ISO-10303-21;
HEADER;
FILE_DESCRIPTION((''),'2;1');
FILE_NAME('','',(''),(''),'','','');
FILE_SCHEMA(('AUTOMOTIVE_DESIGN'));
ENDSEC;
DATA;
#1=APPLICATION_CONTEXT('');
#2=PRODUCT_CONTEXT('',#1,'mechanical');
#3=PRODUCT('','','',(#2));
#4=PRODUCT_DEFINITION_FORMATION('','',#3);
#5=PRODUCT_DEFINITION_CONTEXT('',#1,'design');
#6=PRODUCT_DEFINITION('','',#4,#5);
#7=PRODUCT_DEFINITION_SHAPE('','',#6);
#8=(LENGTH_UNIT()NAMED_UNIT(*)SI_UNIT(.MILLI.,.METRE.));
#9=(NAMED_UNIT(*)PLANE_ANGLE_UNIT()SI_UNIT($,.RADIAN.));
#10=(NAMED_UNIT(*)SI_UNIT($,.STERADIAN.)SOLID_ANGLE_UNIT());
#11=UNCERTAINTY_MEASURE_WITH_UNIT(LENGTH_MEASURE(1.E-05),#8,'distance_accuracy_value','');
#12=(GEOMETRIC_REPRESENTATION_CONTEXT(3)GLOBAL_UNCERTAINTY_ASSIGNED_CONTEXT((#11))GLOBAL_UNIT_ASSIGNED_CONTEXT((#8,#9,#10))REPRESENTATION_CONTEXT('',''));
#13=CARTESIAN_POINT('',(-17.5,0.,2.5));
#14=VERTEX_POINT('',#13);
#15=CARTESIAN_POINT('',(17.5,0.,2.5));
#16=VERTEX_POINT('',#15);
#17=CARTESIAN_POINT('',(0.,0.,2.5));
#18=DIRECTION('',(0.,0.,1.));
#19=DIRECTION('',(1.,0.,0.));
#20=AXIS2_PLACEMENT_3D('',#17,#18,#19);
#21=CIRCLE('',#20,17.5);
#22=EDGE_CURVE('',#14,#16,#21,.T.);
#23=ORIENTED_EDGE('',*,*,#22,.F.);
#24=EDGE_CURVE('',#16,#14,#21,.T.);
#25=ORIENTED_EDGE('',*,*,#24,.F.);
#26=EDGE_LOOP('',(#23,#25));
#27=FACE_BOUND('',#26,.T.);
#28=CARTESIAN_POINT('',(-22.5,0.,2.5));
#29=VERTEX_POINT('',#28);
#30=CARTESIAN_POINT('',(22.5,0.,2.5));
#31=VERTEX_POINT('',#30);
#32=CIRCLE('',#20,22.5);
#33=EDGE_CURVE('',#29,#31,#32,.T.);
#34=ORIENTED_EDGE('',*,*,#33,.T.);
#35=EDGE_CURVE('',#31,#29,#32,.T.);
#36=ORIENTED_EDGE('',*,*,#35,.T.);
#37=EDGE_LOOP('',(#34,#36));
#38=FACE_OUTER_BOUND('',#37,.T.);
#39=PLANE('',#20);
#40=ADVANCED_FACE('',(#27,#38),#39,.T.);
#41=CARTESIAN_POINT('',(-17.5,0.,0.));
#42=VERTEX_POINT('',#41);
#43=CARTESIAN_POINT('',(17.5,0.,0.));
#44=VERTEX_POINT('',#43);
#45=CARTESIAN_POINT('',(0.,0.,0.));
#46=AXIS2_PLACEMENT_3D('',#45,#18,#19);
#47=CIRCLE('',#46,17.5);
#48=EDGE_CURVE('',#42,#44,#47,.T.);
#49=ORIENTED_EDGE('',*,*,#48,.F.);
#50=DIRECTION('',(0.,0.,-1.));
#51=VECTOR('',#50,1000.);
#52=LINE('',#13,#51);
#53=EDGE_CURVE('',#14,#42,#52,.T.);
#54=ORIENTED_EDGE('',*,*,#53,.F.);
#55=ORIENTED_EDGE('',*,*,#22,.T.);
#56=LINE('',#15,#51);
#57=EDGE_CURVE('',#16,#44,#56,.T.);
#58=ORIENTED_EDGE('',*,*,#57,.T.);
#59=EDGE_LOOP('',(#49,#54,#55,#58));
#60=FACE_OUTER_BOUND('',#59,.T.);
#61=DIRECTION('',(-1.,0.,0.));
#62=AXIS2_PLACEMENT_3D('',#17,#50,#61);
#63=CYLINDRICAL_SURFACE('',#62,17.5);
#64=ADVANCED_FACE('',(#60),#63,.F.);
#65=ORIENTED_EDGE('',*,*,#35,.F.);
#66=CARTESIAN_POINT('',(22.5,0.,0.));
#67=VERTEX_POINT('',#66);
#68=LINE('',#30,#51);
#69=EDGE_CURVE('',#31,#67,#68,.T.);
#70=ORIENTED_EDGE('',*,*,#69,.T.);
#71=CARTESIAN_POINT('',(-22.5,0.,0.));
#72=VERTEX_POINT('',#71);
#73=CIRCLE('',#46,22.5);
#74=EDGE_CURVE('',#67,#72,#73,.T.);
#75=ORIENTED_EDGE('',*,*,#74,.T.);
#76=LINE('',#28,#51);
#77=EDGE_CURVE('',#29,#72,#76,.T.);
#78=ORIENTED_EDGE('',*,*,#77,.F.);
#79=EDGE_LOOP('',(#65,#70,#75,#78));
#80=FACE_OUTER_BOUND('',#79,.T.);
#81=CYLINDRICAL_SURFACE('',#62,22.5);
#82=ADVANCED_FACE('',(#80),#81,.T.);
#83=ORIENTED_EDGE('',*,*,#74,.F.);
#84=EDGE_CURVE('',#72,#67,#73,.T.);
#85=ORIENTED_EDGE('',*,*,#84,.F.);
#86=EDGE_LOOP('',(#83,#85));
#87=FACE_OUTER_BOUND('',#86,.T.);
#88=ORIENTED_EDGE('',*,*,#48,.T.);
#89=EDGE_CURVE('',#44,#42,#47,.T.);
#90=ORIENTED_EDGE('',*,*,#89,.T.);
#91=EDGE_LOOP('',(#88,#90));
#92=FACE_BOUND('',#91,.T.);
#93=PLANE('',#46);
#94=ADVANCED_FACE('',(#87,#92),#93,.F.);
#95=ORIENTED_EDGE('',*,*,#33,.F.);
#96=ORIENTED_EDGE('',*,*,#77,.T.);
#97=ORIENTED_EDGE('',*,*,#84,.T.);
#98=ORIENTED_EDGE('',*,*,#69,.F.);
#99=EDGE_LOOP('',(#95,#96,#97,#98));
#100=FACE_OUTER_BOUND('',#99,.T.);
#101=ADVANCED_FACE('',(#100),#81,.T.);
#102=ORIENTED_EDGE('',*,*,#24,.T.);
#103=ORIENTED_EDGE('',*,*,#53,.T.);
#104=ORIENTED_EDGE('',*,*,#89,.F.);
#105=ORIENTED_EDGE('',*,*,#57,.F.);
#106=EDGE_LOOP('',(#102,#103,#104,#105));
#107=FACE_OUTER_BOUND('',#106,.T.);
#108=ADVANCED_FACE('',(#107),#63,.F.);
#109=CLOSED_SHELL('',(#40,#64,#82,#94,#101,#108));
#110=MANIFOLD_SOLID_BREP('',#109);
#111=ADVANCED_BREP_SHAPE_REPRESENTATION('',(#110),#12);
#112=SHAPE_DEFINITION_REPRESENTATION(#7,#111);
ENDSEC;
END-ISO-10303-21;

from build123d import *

# Parameters (mm, degrees)
SKETCH_1_R      = 22.5
SKETCH_1_R_2    = 17.5
EXTRUDE_1_DEPTH = 2.5


with BuildPart() as part:
    # 草图1 → 凸台-拉伸1 (new body)
    with BuildSketch(Plane.XY):
        Circle(SKETCH_1_R)
        Circle(SKETCH_1_R_2, mode=Mode.SUBTRACT)
    extrude(amount=EXTRUDE_1_DEPTH)


solid = part.part
